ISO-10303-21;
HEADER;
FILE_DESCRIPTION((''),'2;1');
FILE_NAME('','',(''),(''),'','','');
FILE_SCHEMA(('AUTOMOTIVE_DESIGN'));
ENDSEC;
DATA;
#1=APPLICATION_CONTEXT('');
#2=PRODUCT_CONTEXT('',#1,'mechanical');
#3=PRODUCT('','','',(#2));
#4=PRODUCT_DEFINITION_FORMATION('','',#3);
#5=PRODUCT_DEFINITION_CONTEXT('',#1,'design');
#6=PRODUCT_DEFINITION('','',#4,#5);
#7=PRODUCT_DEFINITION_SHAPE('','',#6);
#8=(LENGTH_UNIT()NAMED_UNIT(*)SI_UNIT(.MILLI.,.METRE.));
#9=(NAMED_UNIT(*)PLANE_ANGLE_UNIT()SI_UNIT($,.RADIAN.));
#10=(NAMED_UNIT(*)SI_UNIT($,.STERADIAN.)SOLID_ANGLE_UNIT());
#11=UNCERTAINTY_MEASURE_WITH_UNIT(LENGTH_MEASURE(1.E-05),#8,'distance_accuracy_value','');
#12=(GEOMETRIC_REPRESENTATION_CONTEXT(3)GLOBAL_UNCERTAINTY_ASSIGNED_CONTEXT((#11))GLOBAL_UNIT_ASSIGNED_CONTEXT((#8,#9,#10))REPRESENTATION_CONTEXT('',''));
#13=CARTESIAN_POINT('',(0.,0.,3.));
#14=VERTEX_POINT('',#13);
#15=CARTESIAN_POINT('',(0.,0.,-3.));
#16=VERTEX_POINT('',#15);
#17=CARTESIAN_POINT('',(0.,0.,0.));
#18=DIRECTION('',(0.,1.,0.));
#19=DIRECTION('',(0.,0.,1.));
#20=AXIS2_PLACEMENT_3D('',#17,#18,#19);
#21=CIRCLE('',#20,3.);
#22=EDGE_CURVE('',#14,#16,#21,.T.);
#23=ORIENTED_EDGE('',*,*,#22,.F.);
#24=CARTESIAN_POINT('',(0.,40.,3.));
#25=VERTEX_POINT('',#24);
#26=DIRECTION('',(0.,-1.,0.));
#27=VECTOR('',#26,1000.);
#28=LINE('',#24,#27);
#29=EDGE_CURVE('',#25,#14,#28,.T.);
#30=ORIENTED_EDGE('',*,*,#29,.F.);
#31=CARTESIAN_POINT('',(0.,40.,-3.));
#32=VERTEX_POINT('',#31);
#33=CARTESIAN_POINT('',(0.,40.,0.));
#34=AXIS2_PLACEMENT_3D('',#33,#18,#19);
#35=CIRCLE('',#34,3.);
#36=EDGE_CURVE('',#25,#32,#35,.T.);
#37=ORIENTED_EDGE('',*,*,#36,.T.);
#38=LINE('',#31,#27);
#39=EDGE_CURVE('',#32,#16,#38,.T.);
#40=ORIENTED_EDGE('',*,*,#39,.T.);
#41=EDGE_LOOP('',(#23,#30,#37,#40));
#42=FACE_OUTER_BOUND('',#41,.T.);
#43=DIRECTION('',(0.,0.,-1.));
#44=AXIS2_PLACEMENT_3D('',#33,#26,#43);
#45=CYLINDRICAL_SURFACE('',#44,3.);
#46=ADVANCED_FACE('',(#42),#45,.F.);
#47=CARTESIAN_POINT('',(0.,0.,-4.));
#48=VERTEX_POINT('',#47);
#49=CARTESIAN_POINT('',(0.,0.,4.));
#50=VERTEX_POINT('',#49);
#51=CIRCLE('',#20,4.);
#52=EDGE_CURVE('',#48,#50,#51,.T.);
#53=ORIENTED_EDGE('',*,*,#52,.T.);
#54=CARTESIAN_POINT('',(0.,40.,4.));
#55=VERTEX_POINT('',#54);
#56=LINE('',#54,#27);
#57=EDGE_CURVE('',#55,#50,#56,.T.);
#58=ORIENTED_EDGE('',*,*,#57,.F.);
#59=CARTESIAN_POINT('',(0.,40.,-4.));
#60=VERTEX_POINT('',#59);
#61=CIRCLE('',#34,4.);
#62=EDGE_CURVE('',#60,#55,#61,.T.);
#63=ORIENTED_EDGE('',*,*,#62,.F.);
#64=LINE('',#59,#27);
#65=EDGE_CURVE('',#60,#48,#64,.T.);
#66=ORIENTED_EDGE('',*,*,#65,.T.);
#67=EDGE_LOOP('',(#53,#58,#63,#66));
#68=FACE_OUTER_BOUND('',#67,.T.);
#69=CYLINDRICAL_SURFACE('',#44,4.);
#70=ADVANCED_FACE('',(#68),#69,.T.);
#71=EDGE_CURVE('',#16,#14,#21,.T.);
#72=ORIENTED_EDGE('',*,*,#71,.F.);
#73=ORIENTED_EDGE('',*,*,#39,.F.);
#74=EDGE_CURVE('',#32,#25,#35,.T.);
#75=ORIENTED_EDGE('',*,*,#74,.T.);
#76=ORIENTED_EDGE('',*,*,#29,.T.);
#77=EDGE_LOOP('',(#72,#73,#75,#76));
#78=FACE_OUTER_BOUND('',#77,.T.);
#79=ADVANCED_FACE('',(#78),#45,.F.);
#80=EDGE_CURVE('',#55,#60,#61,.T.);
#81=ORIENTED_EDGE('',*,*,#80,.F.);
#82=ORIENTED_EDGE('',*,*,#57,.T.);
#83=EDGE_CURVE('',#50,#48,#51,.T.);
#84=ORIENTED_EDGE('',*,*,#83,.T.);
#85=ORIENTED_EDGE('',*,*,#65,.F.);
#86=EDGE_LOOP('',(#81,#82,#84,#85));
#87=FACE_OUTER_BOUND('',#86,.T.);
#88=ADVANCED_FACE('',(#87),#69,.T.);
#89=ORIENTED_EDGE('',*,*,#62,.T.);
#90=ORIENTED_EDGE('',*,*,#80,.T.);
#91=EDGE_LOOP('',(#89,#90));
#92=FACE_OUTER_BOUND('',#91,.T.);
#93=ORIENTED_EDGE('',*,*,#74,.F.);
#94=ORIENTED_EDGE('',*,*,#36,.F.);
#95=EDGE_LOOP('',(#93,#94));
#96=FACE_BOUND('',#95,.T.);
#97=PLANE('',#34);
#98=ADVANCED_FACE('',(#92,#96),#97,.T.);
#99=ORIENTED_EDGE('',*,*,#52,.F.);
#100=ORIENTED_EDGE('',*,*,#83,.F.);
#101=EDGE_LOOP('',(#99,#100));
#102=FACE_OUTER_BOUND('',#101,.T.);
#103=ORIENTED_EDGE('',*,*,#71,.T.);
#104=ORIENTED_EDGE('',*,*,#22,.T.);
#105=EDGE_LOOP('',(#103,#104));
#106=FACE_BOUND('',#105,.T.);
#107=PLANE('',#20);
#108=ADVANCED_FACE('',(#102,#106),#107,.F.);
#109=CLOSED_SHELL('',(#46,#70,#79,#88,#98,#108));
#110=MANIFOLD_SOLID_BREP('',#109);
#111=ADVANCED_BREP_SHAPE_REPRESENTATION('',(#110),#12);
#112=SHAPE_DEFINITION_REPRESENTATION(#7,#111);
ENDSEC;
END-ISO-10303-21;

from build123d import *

# Parameters (mm, degrees)
SKETCH1_R           = 4
SKETCH1_R_2         = 3
BOSS_EXTRUDE1_DEPTH = 40


with BuildPart() as part:
    # Sketch1 → Boss-Extrude1 (new body)
    with BuildSketch(Plane(origin=(0, 0, 0), x_dir=(1, 0, 0), z_dir=(0, 1, 0))):
        with Locations(Location((0, 0, 0), (0, 0, 270))):
            Circle(SKETCH1_R)
        with Locations(Location((0, 0, 0), (0, 0, 270))):
            Circle(SKETCH1_R_2, mode=Mode.SUBTRACT)
    extrude(amount=BOSS_EXTRUDE1_DEPTH)


solid = part.part
